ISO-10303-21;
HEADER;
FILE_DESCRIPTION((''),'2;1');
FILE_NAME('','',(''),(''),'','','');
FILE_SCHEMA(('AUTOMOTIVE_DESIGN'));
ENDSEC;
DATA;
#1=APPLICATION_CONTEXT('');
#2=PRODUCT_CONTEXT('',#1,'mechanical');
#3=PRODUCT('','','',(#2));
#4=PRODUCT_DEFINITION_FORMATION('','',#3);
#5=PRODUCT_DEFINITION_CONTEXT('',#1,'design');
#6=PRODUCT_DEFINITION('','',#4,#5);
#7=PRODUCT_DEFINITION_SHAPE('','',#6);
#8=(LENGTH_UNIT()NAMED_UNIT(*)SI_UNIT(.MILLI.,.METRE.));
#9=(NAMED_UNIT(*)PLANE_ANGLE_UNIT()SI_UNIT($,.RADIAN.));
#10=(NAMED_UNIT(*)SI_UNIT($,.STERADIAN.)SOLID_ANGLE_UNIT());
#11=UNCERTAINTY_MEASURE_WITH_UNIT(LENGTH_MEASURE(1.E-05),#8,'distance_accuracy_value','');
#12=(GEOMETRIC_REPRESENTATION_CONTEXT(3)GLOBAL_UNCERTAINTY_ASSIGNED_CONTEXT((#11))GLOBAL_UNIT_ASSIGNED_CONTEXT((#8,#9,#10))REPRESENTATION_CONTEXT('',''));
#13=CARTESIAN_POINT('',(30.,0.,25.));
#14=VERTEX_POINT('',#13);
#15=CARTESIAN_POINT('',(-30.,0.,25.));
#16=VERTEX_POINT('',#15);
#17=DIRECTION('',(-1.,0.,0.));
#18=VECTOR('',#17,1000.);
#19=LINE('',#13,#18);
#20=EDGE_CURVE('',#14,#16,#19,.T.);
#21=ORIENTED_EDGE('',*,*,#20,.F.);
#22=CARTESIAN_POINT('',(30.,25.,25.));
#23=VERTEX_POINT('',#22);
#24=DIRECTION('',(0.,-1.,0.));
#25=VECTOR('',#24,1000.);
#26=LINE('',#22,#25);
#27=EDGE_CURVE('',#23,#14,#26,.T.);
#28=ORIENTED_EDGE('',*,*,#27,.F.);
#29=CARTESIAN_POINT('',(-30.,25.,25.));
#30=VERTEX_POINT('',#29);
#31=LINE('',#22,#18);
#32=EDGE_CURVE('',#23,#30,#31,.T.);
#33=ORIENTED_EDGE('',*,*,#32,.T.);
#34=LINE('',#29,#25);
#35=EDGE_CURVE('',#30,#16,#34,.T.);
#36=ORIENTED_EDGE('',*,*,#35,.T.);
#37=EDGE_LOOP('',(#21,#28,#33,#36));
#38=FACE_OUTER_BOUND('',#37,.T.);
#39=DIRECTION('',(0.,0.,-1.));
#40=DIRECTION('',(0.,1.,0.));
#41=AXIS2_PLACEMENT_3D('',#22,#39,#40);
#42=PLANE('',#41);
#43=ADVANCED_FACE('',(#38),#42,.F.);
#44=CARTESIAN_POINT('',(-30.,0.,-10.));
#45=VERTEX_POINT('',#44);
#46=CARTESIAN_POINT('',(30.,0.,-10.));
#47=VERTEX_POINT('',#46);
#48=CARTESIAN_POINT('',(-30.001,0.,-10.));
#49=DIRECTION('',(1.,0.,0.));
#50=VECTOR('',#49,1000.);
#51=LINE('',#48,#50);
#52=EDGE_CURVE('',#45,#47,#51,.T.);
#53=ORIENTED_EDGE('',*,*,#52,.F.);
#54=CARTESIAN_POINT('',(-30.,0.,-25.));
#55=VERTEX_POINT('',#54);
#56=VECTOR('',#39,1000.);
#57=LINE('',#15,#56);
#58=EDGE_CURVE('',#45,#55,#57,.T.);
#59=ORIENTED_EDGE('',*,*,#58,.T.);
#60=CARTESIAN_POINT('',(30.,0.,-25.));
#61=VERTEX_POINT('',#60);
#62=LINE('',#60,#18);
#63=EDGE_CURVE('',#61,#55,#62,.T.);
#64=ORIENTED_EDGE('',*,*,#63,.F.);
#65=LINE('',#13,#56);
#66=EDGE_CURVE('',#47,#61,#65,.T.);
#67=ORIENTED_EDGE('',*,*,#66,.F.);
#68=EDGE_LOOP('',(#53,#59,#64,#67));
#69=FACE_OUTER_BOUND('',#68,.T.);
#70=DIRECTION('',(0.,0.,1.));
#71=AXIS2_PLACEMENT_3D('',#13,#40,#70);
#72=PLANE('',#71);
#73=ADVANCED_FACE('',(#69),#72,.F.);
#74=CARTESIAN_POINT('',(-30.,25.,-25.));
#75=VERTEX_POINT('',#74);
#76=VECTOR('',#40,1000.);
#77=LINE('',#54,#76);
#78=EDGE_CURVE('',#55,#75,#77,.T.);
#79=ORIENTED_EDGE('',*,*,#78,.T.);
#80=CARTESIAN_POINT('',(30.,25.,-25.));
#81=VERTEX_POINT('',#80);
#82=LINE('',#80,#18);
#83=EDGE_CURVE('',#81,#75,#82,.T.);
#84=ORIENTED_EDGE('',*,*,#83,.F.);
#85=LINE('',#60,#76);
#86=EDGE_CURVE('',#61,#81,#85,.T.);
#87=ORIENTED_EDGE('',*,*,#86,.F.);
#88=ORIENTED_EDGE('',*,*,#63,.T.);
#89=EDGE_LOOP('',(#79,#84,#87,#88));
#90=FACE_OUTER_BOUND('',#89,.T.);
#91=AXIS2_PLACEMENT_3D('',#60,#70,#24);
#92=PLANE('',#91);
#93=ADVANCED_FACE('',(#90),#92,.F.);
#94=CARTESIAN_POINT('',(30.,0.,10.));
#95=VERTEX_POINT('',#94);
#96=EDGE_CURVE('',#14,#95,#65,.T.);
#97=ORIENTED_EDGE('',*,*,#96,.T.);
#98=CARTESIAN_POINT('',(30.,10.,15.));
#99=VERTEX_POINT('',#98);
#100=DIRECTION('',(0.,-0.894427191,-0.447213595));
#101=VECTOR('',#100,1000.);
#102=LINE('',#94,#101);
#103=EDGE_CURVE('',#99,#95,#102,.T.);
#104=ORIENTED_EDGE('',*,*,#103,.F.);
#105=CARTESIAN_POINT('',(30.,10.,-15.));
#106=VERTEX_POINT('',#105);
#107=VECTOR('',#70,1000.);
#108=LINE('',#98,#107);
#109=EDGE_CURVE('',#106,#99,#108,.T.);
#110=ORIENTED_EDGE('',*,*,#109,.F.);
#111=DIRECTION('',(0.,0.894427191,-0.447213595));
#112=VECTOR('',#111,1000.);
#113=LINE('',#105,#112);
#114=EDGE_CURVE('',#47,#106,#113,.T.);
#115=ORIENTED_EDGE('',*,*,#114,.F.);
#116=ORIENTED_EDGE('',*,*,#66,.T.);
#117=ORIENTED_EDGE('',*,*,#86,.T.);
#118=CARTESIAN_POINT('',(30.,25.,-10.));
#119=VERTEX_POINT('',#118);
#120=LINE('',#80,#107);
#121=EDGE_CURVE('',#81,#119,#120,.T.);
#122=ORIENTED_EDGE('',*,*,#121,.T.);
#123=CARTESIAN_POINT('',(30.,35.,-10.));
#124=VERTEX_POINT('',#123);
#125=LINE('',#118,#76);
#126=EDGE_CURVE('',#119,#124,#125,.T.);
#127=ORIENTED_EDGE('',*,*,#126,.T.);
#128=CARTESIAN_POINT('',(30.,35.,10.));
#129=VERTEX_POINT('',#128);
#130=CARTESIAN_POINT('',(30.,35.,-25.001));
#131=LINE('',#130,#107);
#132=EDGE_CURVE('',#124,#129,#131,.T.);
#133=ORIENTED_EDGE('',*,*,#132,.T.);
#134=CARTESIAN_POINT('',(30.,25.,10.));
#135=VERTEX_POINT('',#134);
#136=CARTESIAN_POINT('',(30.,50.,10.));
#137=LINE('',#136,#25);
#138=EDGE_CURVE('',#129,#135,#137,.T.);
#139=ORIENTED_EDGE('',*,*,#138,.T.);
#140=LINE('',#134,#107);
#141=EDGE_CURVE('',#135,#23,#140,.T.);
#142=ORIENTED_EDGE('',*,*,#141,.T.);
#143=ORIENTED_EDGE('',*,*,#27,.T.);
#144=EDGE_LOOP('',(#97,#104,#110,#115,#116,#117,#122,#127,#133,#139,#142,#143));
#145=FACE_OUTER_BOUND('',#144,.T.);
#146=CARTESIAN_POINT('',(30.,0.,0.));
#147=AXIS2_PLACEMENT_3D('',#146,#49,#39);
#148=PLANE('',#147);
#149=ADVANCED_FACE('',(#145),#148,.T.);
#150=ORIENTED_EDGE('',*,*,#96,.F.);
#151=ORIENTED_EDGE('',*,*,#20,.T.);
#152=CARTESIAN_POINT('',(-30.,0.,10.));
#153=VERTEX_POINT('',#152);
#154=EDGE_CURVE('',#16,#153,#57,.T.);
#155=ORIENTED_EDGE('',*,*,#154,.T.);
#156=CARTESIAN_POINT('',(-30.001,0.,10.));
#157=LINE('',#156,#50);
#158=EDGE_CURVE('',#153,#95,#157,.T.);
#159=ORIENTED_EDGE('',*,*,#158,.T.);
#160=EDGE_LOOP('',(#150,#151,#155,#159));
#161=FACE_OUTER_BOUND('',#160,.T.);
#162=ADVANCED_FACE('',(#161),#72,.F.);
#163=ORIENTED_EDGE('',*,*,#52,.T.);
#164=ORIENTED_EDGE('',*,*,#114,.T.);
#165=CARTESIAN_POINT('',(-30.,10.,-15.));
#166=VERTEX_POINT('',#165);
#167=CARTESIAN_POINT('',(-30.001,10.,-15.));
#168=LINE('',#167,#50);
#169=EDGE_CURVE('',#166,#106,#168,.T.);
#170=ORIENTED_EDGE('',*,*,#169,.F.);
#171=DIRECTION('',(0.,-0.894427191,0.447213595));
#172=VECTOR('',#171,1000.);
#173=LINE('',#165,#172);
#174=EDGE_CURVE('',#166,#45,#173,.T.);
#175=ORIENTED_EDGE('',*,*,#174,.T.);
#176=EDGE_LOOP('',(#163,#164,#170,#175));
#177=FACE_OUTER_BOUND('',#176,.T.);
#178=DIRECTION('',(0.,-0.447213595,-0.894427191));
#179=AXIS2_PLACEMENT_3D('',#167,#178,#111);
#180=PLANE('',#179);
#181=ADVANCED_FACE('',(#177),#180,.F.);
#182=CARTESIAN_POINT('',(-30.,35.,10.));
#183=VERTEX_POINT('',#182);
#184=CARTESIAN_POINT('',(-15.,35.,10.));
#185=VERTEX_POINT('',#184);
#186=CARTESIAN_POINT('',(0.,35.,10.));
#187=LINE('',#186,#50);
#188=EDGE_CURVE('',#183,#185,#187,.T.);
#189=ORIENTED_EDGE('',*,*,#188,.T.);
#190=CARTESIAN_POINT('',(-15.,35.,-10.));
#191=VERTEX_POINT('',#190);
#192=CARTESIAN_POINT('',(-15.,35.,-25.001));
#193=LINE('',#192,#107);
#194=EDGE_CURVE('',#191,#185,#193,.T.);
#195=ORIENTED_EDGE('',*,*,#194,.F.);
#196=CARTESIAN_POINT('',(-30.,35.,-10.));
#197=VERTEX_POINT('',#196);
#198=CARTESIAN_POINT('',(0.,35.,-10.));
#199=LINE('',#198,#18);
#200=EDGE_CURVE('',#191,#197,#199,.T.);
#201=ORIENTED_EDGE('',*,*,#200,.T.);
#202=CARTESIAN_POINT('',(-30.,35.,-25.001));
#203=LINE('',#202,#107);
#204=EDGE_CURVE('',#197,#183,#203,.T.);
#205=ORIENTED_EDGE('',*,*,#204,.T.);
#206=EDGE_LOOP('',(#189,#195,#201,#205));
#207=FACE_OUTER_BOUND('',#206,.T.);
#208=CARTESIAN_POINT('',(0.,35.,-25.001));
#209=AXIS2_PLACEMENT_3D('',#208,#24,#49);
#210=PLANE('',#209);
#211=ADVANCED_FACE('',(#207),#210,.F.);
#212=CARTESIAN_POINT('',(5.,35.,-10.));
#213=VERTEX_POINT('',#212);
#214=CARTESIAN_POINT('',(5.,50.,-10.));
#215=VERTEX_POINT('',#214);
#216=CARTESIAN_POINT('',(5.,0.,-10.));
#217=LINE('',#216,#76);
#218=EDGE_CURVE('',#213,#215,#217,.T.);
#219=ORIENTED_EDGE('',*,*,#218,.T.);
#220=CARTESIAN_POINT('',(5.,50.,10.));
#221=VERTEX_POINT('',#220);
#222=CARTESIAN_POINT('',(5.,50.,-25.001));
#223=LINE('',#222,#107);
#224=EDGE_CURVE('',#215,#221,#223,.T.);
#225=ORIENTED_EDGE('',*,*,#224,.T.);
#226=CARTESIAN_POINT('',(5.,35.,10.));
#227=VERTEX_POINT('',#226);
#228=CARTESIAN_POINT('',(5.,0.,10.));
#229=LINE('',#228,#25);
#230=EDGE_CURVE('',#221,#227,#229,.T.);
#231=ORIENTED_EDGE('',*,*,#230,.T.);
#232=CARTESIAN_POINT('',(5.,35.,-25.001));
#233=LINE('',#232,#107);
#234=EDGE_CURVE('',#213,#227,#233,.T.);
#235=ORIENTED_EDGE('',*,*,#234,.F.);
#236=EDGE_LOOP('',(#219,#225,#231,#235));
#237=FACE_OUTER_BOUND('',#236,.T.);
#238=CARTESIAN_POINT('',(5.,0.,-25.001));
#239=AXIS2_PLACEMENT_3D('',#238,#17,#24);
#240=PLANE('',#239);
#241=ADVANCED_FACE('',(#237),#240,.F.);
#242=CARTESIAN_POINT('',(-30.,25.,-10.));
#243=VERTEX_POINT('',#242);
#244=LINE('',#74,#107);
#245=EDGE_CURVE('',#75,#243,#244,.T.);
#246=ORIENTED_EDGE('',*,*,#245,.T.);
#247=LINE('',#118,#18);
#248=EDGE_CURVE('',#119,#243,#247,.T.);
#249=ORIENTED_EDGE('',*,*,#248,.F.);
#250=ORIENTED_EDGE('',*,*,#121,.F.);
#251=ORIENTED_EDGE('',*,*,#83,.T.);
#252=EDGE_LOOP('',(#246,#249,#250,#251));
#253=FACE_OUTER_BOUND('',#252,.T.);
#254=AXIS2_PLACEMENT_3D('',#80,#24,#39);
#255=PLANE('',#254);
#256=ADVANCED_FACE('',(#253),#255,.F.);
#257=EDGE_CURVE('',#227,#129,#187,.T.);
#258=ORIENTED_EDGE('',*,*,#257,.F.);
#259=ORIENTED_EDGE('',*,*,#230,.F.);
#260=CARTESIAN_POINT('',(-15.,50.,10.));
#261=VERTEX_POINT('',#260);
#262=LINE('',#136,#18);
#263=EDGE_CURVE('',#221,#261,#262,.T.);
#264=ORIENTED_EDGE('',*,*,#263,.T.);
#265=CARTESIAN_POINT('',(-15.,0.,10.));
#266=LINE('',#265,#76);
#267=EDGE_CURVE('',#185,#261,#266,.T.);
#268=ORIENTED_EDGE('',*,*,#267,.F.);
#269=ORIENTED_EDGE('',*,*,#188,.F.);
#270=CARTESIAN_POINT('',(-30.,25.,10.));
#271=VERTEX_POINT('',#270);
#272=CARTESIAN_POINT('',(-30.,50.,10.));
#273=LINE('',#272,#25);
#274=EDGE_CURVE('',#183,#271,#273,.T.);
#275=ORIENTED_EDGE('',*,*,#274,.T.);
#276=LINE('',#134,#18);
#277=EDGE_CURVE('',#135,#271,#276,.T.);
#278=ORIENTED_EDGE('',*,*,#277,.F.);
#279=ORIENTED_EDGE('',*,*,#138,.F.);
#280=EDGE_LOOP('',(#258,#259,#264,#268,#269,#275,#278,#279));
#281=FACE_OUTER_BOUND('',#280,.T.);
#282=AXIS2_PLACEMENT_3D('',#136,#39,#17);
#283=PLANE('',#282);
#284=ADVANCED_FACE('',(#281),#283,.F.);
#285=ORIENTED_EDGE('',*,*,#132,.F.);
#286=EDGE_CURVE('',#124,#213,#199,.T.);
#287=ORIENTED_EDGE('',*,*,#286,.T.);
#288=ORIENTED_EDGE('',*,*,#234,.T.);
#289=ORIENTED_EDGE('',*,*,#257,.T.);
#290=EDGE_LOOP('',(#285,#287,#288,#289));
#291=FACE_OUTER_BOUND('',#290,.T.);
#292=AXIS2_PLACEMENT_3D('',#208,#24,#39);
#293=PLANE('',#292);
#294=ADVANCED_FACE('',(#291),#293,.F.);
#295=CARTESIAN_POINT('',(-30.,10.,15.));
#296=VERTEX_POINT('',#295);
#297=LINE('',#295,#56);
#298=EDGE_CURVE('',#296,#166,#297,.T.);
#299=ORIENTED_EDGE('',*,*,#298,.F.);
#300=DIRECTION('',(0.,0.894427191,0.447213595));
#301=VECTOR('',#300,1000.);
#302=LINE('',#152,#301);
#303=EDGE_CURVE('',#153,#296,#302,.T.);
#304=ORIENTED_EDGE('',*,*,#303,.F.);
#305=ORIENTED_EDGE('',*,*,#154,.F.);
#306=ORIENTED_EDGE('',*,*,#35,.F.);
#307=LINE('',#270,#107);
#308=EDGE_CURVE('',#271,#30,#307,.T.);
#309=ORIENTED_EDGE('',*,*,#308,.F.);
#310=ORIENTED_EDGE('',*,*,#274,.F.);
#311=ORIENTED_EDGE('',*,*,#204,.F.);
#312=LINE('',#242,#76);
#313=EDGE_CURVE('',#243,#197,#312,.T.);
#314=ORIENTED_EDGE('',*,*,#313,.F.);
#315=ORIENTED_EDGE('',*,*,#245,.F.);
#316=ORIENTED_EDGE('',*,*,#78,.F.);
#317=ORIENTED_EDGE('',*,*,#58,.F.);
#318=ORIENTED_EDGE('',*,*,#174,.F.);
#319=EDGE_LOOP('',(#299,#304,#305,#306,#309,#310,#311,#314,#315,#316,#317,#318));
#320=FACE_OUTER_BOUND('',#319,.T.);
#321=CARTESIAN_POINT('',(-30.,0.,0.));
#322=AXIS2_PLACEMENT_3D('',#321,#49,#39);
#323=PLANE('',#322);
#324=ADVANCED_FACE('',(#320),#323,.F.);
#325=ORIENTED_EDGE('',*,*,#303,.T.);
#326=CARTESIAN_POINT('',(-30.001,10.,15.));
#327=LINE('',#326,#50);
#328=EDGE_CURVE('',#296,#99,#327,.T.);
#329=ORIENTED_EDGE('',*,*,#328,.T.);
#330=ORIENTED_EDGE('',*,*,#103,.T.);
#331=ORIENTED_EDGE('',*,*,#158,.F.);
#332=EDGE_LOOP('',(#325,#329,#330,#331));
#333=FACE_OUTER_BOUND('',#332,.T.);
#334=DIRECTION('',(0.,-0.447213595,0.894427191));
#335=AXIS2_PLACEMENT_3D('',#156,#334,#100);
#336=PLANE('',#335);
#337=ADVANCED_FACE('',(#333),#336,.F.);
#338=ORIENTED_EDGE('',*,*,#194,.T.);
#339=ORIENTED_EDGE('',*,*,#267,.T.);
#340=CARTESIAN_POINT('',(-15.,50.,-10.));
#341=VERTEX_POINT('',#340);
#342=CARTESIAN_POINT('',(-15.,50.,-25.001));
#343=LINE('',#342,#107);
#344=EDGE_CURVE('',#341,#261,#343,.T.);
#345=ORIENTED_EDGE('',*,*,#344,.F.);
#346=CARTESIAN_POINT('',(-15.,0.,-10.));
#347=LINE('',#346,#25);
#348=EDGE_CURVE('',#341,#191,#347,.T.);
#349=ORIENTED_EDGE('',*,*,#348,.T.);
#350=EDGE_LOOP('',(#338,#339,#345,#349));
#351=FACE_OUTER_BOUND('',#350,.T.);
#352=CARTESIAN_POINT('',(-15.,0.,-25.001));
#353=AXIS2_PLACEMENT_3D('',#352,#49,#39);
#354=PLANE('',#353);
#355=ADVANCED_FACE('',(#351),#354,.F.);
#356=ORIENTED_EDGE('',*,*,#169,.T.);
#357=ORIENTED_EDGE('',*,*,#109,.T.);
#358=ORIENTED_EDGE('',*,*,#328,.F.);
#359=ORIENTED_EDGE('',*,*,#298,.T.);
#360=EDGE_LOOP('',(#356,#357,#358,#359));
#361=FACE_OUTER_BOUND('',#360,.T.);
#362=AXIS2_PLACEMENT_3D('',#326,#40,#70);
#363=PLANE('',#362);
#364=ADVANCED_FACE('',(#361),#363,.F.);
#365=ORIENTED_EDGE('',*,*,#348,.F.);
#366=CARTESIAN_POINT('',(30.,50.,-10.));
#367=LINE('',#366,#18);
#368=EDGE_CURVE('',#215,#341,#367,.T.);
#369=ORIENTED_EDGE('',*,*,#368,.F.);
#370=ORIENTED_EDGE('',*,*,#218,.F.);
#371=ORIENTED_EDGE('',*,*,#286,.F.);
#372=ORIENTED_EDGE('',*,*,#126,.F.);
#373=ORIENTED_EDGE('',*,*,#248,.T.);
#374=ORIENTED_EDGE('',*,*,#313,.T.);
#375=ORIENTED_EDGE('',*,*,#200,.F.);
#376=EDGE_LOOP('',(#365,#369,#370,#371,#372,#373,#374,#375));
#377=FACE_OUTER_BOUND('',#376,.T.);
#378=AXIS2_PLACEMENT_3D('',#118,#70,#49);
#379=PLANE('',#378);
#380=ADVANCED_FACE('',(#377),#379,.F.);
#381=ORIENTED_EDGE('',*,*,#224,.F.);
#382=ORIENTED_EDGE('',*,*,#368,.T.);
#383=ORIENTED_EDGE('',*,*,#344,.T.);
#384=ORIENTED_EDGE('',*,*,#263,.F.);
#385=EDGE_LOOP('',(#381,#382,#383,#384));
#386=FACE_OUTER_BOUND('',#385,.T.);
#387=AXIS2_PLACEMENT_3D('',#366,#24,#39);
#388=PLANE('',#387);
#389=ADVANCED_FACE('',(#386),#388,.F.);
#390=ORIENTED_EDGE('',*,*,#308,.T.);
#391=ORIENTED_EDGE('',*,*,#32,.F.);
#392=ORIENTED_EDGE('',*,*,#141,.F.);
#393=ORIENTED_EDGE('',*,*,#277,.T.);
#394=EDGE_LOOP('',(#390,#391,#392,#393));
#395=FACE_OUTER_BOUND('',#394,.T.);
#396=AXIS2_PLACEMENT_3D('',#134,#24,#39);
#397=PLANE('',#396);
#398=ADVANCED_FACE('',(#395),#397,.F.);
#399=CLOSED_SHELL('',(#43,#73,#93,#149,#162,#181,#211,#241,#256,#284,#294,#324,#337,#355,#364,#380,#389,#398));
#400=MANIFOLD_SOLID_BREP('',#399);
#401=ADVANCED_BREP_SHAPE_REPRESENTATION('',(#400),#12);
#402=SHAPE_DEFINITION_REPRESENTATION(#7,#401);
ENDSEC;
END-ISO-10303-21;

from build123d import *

# Parameters (mm, degrees)
STEPPED_BLOCK_60MM_DEPTH             = 30
UNDERSIDE_DOVETAIL_GROOVE_REACH      = 70.007
UNDERSIDE_DOVETAIL_GROOVE_SKETCH_W   = 15
UNDERSIDE_DOVETAIL_GROOVE_SKETCH_H   = 15
UNDERSIDE_DOVETAIL_GROOVE_SKETCH_W_2 = 25
TOP_TIER_POCKET_30X20_REACH          = 84.006


with BuildPart() as part:
    # Stepped Block Profile Sketch → Stepped Block 60mm (new, symmetric)
    with BuildSketch(Plane(origin=(0, 0, 0), x_dir=(0, 0, -1), z_dir=(1, 0, 0))):
        Polygon((-25, 0), (25, 0), (25, 25), (10, 25), (10, 50), (-10, 50), (-10, 25), (-25, 25), align=None)
    extrude(amount=STEPPED_BLOCK_60MM_DEPTH, both=True)

    # Underside Dovetail Groove Sketch → Underside Dovetail Groove (cut, up to next)
    with BuildSketch(Plane.XY.offset(10), mode=Mode.PRIVATE) as underside_dovetail_groove_sk1:
        with Locations((-22.5, 42.5)):
            Rectangle(UNDERSIDE_DOVETAIL_GROOVE_SKETCH_W, UNDERSIDE_DOVETAIL_GROOVE_SKETCH_H)
    underside_dovetail_groove_tool1 = extrude(underside_dovetail_groove_sk1.sketch, amount=-UNDERSIDE_DOVETAIL_GROOVE_REACH, mode=Mode.PRIVATE) & part.part
    # Underside Dovetail Groove Sketch → Underside Dovetail Groove (cut, up to next)
    with BuildSketch(Plane.XY.offset(10), mode=Mode.PRIVATE) as underside_dovetail_groove_sk2:
        with Locations((17.5, 42.5)):
            Rectangle(UNDERSIDE_DOVETAIL_GROOVE_SKETCH_W_2, UNDERSIDE_DOVETAIL_GROOVE_SKETCH_H)
    underside_dovetail_groove_tool2 = extrude(underside_dovetail_groove_sk2.sketch, amount=-UNDERSIDE_DOVETAIL_GROOVE_REACH, mode=Mode.PRIVATE) & part.part
    add(underside_dovetail_groove_tool1.solids().sort_by_distance((-22.5, 42.5, 10))[0], mode=Mode.SUBTRACT)
    add(underside_dovetail_groove_tool2.solids().sort_by_distance((17.5, 42.5, 10))[0], mode=Mode.SUBTRACT)

    # Top Tier Pocket Sketch → Top Tier Pocket 30x20 (cut, up to next)
    with BuildSketch(Plane(origin=(30, 0, 0), x_dir=(0, 0, -1), z_dir=(1, 0, 0)), mode=Mode.PRIVATE) as top_tier_pocket_30x20_sk1:
        Polygon((-10, 0), (-15, 10), (15, 10), (10, 0), align=None)
    top_tier_pocket_30x20_tool1 = extrude(top_tier_pocket_30x20_sk1.sketch, amount=-TOP_TIER_POCKET_30X20_REACH, mode=Mode.PRIVATE) & part.part
    add(top_tier_pocket_30x20_tool1.solids().sort_by_distance((30, 5.333333, 0))[0], mode=Mode.SUBTRACT)


solid = part.part
